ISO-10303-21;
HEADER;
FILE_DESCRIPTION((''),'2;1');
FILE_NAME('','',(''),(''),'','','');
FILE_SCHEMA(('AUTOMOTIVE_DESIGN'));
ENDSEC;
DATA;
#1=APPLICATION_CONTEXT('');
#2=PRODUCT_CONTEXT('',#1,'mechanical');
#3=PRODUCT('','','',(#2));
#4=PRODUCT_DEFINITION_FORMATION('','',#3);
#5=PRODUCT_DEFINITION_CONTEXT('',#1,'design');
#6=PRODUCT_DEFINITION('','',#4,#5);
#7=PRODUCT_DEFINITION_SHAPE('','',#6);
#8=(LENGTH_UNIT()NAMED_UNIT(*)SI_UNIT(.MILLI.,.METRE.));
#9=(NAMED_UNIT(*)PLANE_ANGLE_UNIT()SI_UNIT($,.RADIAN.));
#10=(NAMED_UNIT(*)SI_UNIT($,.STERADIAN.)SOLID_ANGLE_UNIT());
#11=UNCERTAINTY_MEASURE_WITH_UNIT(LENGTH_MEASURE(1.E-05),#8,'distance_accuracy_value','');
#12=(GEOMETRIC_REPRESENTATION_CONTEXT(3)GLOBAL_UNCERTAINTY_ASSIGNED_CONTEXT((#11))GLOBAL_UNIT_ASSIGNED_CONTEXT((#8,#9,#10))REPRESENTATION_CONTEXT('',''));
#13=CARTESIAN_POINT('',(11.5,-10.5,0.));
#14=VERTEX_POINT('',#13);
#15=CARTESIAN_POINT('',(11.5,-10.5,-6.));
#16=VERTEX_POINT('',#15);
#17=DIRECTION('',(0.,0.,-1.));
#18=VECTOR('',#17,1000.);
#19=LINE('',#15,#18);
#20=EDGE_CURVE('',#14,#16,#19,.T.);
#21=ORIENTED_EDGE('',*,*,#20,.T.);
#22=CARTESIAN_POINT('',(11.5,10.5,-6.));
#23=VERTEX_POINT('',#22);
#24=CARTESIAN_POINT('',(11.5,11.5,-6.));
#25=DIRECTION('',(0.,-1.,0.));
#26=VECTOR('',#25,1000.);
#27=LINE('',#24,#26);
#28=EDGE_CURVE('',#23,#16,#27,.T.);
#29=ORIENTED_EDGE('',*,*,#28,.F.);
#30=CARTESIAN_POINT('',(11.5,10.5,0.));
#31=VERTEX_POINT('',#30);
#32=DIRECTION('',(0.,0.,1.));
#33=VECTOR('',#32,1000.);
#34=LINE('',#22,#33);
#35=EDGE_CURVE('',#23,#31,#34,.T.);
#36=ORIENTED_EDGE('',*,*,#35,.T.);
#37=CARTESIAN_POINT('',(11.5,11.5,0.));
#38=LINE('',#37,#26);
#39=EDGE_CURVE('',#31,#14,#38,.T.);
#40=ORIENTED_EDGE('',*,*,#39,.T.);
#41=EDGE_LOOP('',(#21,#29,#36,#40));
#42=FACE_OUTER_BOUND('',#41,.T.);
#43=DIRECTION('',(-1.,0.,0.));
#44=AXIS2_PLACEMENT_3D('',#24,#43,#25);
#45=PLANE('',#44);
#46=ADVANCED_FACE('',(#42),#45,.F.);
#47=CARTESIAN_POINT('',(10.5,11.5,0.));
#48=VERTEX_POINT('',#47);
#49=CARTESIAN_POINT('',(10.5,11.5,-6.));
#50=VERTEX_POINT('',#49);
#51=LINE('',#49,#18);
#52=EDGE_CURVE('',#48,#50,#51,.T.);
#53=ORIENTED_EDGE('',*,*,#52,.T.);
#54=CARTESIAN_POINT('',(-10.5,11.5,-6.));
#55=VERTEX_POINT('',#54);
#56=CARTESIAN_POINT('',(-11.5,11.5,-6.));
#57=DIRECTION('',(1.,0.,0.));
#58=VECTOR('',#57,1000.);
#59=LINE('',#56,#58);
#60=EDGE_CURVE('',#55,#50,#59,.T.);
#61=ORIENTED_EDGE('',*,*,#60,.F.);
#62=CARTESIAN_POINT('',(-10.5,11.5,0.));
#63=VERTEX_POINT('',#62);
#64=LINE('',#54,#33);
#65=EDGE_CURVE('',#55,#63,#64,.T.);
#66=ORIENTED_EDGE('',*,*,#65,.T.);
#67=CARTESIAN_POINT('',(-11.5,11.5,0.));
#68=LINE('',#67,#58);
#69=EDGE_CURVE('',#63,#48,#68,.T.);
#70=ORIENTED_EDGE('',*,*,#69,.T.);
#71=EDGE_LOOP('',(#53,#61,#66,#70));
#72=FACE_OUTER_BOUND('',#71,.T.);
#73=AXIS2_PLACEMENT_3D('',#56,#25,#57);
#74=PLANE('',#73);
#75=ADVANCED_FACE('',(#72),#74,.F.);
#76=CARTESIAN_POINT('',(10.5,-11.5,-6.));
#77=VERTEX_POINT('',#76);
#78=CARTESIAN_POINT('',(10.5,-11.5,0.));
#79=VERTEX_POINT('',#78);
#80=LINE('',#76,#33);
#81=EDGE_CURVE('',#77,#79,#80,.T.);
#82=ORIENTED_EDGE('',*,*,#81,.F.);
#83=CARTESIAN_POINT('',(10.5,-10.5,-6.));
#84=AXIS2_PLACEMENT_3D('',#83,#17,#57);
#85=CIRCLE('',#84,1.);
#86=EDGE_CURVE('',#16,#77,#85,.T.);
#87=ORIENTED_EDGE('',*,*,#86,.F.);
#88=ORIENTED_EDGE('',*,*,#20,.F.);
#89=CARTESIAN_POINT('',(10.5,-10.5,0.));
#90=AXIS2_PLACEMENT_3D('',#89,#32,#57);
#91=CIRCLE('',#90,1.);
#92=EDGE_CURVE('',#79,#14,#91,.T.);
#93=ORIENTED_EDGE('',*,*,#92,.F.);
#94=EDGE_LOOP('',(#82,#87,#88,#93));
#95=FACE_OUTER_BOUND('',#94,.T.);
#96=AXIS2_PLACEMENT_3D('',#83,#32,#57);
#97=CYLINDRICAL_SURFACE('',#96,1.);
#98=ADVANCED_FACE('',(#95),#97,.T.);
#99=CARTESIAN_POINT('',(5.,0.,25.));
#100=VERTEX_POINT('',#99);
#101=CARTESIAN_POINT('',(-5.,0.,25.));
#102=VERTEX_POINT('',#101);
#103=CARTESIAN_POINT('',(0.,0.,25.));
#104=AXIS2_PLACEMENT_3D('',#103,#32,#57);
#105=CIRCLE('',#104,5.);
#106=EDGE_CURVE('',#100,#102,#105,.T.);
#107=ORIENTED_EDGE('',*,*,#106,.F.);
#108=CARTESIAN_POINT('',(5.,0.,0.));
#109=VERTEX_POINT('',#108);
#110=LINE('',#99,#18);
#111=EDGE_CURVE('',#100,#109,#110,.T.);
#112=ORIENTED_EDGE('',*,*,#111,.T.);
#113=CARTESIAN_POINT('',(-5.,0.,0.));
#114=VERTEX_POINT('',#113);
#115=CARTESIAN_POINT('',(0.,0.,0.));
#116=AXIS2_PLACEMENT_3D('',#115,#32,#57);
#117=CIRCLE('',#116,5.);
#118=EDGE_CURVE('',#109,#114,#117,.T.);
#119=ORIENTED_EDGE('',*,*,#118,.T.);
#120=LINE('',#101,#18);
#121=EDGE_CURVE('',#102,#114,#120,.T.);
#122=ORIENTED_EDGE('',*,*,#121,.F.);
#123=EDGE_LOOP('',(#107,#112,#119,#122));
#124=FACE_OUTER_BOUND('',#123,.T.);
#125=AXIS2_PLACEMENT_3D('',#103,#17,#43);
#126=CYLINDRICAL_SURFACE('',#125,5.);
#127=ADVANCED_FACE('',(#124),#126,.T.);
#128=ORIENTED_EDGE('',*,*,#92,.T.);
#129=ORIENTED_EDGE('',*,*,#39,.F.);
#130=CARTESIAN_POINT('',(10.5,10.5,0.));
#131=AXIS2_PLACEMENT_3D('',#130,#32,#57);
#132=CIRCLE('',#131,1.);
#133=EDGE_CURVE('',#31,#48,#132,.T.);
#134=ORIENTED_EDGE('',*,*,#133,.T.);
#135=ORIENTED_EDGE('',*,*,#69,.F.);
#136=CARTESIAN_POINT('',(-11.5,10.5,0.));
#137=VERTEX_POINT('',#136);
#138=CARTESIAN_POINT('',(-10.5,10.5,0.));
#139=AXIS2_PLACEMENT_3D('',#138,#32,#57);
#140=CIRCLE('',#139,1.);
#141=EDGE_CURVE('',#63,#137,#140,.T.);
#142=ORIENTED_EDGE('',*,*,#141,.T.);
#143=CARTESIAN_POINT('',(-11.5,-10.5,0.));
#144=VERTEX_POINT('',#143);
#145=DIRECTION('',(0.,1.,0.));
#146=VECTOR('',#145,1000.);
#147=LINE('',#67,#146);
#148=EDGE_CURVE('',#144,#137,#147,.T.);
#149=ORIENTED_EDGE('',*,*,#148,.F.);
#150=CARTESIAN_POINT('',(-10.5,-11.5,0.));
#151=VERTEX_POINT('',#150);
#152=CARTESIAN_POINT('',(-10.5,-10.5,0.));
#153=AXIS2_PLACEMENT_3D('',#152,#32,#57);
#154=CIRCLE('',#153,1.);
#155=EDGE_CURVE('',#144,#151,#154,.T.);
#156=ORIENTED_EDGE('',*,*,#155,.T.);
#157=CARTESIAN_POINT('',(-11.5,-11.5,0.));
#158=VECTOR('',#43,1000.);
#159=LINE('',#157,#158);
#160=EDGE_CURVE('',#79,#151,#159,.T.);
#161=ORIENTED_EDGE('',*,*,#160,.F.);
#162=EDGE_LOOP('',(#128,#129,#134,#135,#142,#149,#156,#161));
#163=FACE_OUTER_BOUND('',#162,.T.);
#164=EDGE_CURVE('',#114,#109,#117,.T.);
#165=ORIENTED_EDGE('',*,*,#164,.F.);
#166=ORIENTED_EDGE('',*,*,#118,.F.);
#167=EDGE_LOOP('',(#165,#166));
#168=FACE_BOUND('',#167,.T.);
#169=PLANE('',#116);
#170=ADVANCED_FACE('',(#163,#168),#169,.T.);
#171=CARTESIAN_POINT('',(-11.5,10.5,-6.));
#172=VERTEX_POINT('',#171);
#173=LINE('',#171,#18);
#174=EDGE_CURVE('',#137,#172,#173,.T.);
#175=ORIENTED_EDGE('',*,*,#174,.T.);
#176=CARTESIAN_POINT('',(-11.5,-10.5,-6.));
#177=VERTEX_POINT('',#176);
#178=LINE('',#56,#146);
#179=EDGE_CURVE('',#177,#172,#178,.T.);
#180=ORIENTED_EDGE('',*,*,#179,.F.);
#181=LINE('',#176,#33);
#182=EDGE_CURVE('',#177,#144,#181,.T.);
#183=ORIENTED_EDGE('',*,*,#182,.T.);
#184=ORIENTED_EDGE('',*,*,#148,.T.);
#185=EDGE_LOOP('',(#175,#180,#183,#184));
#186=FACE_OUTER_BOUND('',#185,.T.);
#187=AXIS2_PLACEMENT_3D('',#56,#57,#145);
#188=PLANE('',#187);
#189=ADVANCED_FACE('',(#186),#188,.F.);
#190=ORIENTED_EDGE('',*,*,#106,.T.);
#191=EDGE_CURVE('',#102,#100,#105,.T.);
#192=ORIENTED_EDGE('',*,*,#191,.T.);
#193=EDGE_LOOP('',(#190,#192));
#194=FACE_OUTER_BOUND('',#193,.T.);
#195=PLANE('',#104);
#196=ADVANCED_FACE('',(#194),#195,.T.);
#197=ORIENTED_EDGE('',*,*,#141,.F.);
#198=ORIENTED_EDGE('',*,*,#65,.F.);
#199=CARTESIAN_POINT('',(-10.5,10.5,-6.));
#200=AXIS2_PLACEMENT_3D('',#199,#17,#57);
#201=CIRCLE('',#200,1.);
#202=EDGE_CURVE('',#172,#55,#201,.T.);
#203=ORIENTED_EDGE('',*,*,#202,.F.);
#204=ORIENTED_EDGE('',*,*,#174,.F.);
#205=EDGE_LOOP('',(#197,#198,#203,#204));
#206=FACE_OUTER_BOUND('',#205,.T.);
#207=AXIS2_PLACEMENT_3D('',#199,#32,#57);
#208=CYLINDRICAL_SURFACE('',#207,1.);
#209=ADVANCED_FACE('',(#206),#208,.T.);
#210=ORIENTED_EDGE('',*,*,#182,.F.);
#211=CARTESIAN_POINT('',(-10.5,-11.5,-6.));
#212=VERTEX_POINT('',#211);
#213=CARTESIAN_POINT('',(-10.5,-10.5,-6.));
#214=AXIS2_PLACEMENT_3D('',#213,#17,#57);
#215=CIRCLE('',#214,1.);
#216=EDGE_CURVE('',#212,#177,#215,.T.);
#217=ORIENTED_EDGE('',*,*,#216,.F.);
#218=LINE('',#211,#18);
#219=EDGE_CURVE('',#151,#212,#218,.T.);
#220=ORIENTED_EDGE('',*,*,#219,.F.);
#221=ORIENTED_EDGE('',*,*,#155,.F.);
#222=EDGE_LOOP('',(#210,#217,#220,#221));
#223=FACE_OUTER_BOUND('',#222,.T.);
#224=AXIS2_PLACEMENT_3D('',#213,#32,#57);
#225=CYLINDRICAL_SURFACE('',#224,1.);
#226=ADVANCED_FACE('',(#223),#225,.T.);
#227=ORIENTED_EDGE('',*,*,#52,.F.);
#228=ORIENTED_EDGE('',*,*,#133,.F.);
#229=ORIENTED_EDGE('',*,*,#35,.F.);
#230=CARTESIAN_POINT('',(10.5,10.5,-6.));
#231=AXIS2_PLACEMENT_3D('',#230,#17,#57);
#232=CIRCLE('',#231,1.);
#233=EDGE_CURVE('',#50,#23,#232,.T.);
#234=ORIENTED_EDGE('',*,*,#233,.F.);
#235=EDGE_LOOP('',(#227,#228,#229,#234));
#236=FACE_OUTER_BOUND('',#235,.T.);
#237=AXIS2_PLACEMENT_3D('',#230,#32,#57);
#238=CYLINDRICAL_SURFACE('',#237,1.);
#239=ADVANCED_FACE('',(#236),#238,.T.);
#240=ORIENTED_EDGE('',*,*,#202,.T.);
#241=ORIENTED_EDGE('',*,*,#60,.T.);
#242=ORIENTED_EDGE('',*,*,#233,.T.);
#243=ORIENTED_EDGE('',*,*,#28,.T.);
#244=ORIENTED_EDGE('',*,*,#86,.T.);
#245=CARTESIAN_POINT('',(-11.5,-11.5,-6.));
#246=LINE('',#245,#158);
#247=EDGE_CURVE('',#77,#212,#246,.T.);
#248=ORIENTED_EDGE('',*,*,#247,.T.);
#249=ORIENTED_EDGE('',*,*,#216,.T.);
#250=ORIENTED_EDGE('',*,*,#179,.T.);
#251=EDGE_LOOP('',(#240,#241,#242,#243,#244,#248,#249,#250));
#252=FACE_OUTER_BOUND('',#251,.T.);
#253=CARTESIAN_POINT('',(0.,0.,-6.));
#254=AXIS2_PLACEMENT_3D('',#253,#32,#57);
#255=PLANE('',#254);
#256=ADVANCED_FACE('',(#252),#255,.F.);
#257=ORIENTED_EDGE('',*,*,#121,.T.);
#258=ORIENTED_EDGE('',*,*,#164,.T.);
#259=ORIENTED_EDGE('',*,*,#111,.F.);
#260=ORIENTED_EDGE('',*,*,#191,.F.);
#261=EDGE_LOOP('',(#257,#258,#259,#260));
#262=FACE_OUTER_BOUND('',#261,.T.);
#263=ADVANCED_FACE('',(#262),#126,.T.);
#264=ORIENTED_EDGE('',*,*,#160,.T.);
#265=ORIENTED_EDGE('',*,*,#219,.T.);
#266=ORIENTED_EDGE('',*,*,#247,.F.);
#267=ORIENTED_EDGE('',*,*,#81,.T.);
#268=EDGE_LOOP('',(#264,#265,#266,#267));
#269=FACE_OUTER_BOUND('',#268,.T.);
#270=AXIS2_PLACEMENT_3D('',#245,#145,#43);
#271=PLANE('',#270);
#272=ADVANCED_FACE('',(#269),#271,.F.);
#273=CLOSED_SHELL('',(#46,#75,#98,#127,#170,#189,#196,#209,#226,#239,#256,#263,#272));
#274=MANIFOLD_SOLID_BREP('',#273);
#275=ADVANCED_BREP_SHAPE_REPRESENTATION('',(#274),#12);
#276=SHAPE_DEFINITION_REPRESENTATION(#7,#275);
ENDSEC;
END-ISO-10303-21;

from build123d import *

# Parameters (mm, degrees)
SKETCH_1_R      = 5
EXTRUDE_1_DEPTH = 25
SKETCH_2_W      = 23
SKETCH_2_H      = 23
EXTRUDE_2_DEPTH = 6
FILLET_1_R      = 1


with BuildPart() as part:
    # 草图1 → 凸台-拉伸1 (new body)
    with BuildSketch(Plane.XY):
        Circle(SKETCH_1_R)
    extrude(amount=EXTRUDE_1_DEPTH)

    # 草图2 → 凸台-拉伸2 (add)
    with BuildSketch(Plane(origin=(0, 0, 0), x_dir=(-1, 0, 0), z_dir=(0, 0, -1))):
        Rectangle(SKETCH_2_W, SKETCH_2_H)
    extrude(amount=EXTRUDE_2_DEPTH)

    # 圆角1
    fillet_1_edges = [part.edges().sort_by_distance(p)[0] for p in [
        (11.5, 11.5, -3),
        (11.5, -11.5, -3),
        (-11.5, -11.5, -3),
        (-11.5, 11.5, -3),
    ]]
    fillet(fillet_1_edges, radius=FILLET_1_R)


solid = part.part
